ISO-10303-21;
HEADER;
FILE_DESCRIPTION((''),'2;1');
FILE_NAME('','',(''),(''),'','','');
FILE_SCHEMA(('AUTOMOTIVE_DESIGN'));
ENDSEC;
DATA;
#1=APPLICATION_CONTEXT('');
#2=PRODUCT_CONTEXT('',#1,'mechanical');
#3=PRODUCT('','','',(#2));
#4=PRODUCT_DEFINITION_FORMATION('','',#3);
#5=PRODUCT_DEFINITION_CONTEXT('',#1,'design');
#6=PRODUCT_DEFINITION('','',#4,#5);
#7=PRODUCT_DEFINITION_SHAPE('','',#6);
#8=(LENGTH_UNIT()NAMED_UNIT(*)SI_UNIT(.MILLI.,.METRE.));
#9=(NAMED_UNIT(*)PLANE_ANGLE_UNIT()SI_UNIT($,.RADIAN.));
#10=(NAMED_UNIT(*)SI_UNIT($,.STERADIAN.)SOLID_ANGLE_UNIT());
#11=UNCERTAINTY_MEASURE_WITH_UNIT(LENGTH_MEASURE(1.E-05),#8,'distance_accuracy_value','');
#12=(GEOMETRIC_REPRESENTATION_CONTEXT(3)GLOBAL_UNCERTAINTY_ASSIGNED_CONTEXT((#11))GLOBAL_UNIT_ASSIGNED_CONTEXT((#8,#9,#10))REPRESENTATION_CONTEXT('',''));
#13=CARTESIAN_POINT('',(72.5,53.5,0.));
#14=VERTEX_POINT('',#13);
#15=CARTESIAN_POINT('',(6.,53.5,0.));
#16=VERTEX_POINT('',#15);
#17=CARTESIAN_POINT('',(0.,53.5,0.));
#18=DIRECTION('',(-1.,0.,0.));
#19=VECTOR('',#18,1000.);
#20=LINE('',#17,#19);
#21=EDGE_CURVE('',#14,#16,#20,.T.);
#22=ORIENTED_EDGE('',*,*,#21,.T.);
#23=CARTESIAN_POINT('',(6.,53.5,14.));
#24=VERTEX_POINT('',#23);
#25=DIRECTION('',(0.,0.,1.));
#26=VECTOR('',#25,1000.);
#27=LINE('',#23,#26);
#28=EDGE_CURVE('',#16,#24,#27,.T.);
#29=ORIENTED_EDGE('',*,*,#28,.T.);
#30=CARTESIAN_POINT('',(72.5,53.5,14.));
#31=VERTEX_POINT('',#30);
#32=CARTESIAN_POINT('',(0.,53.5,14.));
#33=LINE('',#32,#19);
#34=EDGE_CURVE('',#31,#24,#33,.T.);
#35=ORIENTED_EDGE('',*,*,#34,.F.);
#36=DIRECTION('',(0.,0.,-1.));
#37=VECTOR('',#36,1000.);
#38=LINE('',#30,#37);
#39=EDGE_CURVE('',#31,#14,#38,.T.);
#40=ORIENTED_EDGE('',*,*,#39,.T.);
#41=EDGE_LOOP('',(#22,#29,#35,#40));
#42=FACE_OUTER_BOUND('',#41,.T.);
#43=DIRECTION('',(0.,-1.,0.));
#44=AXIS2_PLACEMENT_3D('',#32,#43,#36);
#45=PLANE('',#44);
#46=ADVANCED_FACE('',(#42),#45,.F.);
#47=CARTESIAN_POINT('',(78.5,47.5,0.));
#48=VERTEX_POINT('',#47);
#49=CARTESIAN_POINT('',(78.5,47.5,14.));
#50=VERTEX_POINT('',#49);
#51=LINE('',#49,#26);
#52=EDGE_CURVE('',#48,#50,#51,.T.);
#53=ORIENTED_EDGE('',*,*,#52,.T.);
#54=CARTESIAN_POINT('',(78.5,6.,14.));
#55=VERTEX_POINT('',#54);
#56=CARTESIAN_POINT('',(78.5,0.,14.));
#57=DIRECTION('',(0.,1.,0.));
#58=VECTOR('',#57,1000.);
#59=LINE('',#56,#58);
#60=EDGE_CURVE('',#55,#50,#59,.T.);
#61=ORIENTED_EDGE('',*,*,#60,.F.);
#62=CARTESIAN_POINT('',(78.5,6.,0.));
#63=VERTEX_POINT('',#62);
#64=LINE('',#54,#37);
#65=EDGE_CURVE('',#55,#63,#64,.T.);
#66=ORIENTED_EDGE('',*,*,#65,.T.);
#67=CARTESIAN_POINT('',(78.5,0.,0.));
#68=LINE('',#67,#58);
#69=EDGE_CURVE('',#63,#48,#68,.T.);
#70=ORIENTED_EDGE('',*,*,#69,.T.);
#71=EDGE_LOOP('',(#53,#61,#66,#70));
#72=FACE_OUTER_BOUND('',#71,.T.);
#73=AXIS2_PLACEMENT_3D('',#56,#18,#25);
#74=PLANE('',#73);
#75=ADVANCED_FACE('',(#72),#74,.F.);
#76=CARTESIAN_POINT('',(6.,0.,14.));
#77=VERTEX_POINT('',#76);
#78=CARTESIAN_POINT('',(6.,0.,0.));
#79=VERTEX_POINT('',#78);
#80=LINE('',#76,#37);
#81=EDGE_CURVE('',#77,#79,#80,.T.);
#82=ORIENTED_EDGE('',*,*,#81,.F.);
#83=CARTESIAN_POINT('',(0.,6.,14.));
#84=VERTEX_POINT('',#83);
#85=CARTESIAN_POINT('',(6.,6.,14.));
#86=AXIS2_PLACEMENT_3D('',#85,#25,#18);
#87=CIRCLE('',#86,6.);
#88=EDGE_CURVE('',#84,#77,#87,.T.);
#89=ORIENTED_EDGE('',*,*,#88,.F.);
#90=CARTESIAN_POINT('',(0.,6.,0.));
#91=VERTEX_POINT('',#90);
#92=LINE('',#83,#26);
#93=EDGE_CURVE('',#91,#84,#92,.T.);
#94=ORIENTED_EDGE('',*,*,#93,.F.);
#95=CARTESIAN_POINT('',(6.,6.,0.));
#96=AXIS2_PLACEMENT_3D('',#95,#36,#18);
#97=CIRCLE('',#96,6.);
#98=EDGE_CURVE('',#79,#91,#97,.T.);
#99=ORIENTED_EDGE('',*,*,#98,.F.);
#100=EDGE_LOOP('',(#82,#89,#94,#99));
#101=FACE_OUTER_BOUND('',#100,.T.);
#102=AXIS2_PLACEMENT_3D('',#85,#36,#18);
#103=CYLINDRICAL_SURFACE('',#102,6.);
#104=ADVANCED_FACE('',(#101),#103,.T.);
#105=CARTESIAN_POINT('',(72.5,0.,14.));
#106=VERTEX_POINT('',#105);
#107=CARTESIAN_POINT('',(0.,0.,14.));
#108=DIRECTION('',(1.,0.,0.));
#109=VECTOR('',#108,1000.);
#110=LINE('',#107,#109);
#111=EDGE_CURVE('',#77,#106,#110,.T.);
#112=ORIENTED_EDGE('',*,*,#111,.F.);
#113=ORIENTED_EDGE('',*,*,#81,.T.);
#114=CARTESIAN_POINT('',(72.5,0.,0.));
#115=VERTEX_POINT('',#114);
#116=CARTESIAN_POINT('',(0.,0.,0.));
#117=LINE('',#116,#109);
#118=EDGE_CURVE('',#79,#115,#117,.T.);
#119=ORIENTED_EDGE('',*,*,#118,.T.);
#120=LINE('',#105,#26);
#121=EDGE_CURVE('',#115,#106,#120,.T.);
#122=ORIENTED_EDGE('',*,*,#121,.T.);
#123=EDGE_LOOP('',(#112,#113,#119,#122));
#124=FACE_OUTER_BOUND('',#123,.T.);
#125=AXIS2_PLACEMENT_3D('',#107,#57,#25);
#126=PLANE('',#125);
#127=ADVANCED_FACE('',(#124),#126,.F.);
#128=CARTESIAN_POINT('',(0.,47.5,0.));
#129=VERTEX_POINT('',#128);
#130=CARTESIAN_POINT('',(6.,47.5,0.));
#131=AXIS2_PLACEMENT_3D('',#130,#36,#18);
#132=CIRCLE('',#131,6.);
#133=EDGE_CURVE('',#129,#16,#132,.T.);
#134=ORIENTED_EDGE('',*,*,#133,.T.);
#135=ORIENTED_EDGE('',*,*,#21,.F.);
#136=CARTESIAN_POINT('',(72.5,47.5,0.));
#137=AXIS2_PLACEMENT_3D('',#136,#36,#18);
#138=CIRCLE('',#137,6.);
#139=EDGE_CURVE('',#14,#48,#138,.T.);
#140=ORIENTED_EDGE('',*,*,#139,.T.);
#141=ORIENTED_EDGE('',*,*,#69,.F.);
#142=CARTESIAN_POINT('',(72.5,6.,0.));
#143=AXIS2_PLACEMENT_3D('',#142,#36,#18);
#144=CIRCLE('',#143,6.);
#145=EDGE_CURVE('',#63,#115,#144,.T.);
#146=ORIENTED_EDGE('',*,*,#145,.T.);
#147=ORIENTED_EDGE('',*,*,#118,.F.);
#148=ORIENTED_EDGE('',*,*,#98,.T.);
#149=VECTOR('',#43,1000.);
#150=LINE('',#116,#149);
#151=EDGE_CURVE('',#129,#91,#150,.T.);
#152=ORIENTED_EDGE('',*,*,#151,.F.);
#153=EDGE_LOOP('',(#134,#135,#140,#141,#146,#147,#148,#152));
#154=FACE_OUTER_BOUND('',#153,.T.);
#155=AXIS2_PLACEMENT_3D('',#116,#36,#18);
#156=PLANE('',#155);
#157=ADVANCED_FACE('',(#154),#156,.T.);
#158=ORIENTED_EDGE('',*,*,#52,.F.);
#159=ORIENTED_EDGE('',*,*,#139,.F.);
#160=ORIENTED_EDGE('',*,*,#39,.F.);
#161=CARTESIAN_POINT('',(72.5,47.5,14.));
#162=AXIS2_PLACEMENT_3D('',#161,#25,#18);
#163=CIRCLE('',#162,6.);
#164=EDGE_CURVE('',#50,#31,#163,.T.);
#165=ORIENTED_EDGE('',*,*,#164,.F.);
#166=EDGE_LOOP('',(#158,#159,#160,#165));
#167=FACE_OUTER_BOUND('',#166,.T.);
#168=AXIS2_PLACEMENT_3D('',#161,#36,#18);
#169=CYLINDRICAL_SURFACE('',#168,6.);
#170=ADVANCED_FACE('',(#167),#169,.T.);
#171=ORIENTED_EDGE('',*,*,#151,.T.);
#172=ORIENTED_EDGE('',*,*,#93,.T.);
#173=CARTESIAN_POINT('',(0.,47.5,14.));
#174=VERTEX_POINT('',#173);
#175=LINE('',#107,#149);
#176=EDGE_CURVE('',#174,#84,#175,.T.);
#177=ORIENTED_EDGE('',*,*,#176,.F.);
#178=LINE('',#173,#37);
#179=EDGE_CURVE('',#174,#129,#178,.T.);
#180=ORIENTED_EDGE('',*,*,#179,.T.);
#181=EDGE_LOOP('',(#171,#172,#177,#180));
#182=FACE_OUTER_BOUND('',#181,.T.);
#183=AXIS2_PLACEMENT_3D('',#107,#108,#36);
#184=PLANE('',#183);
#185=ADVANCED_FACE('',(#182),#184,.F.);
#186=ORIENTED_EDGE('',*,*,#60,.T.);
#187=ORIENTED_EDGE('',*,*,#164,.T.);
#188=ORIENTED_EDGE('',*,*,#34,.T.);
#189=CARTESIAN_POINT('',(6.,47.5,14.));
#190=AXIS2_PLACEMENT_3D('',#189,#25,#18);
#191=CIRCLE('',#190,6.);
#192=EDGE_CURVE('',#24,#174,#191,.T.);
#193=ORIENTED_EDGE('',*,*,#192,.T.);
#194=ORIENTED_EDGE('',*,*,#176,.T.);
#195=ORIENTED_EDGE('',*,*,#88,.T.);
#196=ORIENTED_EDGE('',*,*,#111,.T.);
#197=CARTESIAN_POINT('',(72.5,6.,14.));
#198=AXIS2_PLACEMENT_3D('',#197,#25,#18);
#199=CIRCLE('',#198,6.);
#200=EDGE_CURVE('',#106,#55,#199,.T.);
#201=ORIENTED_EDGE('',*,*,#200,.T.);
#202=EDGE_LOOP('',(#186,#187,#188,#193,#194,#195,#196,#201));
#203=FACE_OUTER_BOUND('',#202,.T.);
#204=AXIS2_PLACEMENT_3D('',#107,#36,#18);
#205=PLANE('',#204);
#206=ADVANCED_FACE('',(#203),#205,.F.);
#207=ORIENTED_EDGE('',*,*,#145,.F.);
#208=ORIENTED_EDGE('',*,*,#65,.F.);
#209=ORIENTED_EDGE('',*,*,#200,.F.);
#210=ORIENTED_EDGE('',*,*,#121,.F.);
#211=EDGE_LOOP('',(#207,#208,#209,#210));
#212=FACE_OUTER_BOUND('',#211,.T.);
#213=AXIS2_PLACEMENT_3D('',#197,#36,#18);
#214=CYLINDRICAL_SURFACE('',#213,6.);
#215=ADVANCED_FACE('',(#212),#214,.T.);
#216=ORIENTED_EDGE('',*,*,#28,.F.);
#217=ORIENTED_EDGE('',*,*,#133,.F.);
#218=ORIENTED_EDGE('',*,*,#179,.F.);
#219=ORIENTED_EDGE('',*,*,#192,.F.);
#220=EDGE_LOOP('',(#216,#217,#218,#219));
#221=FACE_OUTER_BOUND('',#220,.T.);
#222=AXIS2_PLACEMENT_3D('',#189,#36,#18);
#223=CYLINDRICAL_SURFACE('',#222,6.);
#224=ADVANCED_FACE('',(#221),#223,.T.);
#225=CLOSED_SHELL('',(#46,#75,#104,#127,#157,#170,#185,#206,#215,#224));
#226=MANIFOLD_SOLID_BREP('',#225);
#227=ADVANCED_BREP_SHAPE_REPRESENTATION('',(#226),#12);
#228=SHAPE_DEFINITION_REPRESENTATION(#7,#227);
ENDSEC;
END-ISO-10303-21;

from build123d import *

# Parameters (mm, degrees)
SKETCH_1_W      = 78.5
SKETCH_1_H      = 53.5
EXTRUDE_1_DEPTH = 14
FILLET_1_R      = 6


with BuildPart() as part:
    # 草图1 → 凸台-拉伸1 (new body)
    with BuildSketch(Plane.XY):
        with Locations((39.25, 26.75)):
            Rectangle(SKETCH_1_W, SKETCH_1_H)
    extrude(amount=EXTRUDE_1_DEPTH)

    # 圆角1
    fillet_1_edges = [part.edges().sort_by_distance(p)[0] for p in [
        (0, 53.5, 7),
        (78.5, 53.5, 7),
        (78.5, 0, 7),
        (0, 0, 7),
    ]]
    fillet(fillet_1_edges, radius=FILLET_1_R)


solid = part.part
